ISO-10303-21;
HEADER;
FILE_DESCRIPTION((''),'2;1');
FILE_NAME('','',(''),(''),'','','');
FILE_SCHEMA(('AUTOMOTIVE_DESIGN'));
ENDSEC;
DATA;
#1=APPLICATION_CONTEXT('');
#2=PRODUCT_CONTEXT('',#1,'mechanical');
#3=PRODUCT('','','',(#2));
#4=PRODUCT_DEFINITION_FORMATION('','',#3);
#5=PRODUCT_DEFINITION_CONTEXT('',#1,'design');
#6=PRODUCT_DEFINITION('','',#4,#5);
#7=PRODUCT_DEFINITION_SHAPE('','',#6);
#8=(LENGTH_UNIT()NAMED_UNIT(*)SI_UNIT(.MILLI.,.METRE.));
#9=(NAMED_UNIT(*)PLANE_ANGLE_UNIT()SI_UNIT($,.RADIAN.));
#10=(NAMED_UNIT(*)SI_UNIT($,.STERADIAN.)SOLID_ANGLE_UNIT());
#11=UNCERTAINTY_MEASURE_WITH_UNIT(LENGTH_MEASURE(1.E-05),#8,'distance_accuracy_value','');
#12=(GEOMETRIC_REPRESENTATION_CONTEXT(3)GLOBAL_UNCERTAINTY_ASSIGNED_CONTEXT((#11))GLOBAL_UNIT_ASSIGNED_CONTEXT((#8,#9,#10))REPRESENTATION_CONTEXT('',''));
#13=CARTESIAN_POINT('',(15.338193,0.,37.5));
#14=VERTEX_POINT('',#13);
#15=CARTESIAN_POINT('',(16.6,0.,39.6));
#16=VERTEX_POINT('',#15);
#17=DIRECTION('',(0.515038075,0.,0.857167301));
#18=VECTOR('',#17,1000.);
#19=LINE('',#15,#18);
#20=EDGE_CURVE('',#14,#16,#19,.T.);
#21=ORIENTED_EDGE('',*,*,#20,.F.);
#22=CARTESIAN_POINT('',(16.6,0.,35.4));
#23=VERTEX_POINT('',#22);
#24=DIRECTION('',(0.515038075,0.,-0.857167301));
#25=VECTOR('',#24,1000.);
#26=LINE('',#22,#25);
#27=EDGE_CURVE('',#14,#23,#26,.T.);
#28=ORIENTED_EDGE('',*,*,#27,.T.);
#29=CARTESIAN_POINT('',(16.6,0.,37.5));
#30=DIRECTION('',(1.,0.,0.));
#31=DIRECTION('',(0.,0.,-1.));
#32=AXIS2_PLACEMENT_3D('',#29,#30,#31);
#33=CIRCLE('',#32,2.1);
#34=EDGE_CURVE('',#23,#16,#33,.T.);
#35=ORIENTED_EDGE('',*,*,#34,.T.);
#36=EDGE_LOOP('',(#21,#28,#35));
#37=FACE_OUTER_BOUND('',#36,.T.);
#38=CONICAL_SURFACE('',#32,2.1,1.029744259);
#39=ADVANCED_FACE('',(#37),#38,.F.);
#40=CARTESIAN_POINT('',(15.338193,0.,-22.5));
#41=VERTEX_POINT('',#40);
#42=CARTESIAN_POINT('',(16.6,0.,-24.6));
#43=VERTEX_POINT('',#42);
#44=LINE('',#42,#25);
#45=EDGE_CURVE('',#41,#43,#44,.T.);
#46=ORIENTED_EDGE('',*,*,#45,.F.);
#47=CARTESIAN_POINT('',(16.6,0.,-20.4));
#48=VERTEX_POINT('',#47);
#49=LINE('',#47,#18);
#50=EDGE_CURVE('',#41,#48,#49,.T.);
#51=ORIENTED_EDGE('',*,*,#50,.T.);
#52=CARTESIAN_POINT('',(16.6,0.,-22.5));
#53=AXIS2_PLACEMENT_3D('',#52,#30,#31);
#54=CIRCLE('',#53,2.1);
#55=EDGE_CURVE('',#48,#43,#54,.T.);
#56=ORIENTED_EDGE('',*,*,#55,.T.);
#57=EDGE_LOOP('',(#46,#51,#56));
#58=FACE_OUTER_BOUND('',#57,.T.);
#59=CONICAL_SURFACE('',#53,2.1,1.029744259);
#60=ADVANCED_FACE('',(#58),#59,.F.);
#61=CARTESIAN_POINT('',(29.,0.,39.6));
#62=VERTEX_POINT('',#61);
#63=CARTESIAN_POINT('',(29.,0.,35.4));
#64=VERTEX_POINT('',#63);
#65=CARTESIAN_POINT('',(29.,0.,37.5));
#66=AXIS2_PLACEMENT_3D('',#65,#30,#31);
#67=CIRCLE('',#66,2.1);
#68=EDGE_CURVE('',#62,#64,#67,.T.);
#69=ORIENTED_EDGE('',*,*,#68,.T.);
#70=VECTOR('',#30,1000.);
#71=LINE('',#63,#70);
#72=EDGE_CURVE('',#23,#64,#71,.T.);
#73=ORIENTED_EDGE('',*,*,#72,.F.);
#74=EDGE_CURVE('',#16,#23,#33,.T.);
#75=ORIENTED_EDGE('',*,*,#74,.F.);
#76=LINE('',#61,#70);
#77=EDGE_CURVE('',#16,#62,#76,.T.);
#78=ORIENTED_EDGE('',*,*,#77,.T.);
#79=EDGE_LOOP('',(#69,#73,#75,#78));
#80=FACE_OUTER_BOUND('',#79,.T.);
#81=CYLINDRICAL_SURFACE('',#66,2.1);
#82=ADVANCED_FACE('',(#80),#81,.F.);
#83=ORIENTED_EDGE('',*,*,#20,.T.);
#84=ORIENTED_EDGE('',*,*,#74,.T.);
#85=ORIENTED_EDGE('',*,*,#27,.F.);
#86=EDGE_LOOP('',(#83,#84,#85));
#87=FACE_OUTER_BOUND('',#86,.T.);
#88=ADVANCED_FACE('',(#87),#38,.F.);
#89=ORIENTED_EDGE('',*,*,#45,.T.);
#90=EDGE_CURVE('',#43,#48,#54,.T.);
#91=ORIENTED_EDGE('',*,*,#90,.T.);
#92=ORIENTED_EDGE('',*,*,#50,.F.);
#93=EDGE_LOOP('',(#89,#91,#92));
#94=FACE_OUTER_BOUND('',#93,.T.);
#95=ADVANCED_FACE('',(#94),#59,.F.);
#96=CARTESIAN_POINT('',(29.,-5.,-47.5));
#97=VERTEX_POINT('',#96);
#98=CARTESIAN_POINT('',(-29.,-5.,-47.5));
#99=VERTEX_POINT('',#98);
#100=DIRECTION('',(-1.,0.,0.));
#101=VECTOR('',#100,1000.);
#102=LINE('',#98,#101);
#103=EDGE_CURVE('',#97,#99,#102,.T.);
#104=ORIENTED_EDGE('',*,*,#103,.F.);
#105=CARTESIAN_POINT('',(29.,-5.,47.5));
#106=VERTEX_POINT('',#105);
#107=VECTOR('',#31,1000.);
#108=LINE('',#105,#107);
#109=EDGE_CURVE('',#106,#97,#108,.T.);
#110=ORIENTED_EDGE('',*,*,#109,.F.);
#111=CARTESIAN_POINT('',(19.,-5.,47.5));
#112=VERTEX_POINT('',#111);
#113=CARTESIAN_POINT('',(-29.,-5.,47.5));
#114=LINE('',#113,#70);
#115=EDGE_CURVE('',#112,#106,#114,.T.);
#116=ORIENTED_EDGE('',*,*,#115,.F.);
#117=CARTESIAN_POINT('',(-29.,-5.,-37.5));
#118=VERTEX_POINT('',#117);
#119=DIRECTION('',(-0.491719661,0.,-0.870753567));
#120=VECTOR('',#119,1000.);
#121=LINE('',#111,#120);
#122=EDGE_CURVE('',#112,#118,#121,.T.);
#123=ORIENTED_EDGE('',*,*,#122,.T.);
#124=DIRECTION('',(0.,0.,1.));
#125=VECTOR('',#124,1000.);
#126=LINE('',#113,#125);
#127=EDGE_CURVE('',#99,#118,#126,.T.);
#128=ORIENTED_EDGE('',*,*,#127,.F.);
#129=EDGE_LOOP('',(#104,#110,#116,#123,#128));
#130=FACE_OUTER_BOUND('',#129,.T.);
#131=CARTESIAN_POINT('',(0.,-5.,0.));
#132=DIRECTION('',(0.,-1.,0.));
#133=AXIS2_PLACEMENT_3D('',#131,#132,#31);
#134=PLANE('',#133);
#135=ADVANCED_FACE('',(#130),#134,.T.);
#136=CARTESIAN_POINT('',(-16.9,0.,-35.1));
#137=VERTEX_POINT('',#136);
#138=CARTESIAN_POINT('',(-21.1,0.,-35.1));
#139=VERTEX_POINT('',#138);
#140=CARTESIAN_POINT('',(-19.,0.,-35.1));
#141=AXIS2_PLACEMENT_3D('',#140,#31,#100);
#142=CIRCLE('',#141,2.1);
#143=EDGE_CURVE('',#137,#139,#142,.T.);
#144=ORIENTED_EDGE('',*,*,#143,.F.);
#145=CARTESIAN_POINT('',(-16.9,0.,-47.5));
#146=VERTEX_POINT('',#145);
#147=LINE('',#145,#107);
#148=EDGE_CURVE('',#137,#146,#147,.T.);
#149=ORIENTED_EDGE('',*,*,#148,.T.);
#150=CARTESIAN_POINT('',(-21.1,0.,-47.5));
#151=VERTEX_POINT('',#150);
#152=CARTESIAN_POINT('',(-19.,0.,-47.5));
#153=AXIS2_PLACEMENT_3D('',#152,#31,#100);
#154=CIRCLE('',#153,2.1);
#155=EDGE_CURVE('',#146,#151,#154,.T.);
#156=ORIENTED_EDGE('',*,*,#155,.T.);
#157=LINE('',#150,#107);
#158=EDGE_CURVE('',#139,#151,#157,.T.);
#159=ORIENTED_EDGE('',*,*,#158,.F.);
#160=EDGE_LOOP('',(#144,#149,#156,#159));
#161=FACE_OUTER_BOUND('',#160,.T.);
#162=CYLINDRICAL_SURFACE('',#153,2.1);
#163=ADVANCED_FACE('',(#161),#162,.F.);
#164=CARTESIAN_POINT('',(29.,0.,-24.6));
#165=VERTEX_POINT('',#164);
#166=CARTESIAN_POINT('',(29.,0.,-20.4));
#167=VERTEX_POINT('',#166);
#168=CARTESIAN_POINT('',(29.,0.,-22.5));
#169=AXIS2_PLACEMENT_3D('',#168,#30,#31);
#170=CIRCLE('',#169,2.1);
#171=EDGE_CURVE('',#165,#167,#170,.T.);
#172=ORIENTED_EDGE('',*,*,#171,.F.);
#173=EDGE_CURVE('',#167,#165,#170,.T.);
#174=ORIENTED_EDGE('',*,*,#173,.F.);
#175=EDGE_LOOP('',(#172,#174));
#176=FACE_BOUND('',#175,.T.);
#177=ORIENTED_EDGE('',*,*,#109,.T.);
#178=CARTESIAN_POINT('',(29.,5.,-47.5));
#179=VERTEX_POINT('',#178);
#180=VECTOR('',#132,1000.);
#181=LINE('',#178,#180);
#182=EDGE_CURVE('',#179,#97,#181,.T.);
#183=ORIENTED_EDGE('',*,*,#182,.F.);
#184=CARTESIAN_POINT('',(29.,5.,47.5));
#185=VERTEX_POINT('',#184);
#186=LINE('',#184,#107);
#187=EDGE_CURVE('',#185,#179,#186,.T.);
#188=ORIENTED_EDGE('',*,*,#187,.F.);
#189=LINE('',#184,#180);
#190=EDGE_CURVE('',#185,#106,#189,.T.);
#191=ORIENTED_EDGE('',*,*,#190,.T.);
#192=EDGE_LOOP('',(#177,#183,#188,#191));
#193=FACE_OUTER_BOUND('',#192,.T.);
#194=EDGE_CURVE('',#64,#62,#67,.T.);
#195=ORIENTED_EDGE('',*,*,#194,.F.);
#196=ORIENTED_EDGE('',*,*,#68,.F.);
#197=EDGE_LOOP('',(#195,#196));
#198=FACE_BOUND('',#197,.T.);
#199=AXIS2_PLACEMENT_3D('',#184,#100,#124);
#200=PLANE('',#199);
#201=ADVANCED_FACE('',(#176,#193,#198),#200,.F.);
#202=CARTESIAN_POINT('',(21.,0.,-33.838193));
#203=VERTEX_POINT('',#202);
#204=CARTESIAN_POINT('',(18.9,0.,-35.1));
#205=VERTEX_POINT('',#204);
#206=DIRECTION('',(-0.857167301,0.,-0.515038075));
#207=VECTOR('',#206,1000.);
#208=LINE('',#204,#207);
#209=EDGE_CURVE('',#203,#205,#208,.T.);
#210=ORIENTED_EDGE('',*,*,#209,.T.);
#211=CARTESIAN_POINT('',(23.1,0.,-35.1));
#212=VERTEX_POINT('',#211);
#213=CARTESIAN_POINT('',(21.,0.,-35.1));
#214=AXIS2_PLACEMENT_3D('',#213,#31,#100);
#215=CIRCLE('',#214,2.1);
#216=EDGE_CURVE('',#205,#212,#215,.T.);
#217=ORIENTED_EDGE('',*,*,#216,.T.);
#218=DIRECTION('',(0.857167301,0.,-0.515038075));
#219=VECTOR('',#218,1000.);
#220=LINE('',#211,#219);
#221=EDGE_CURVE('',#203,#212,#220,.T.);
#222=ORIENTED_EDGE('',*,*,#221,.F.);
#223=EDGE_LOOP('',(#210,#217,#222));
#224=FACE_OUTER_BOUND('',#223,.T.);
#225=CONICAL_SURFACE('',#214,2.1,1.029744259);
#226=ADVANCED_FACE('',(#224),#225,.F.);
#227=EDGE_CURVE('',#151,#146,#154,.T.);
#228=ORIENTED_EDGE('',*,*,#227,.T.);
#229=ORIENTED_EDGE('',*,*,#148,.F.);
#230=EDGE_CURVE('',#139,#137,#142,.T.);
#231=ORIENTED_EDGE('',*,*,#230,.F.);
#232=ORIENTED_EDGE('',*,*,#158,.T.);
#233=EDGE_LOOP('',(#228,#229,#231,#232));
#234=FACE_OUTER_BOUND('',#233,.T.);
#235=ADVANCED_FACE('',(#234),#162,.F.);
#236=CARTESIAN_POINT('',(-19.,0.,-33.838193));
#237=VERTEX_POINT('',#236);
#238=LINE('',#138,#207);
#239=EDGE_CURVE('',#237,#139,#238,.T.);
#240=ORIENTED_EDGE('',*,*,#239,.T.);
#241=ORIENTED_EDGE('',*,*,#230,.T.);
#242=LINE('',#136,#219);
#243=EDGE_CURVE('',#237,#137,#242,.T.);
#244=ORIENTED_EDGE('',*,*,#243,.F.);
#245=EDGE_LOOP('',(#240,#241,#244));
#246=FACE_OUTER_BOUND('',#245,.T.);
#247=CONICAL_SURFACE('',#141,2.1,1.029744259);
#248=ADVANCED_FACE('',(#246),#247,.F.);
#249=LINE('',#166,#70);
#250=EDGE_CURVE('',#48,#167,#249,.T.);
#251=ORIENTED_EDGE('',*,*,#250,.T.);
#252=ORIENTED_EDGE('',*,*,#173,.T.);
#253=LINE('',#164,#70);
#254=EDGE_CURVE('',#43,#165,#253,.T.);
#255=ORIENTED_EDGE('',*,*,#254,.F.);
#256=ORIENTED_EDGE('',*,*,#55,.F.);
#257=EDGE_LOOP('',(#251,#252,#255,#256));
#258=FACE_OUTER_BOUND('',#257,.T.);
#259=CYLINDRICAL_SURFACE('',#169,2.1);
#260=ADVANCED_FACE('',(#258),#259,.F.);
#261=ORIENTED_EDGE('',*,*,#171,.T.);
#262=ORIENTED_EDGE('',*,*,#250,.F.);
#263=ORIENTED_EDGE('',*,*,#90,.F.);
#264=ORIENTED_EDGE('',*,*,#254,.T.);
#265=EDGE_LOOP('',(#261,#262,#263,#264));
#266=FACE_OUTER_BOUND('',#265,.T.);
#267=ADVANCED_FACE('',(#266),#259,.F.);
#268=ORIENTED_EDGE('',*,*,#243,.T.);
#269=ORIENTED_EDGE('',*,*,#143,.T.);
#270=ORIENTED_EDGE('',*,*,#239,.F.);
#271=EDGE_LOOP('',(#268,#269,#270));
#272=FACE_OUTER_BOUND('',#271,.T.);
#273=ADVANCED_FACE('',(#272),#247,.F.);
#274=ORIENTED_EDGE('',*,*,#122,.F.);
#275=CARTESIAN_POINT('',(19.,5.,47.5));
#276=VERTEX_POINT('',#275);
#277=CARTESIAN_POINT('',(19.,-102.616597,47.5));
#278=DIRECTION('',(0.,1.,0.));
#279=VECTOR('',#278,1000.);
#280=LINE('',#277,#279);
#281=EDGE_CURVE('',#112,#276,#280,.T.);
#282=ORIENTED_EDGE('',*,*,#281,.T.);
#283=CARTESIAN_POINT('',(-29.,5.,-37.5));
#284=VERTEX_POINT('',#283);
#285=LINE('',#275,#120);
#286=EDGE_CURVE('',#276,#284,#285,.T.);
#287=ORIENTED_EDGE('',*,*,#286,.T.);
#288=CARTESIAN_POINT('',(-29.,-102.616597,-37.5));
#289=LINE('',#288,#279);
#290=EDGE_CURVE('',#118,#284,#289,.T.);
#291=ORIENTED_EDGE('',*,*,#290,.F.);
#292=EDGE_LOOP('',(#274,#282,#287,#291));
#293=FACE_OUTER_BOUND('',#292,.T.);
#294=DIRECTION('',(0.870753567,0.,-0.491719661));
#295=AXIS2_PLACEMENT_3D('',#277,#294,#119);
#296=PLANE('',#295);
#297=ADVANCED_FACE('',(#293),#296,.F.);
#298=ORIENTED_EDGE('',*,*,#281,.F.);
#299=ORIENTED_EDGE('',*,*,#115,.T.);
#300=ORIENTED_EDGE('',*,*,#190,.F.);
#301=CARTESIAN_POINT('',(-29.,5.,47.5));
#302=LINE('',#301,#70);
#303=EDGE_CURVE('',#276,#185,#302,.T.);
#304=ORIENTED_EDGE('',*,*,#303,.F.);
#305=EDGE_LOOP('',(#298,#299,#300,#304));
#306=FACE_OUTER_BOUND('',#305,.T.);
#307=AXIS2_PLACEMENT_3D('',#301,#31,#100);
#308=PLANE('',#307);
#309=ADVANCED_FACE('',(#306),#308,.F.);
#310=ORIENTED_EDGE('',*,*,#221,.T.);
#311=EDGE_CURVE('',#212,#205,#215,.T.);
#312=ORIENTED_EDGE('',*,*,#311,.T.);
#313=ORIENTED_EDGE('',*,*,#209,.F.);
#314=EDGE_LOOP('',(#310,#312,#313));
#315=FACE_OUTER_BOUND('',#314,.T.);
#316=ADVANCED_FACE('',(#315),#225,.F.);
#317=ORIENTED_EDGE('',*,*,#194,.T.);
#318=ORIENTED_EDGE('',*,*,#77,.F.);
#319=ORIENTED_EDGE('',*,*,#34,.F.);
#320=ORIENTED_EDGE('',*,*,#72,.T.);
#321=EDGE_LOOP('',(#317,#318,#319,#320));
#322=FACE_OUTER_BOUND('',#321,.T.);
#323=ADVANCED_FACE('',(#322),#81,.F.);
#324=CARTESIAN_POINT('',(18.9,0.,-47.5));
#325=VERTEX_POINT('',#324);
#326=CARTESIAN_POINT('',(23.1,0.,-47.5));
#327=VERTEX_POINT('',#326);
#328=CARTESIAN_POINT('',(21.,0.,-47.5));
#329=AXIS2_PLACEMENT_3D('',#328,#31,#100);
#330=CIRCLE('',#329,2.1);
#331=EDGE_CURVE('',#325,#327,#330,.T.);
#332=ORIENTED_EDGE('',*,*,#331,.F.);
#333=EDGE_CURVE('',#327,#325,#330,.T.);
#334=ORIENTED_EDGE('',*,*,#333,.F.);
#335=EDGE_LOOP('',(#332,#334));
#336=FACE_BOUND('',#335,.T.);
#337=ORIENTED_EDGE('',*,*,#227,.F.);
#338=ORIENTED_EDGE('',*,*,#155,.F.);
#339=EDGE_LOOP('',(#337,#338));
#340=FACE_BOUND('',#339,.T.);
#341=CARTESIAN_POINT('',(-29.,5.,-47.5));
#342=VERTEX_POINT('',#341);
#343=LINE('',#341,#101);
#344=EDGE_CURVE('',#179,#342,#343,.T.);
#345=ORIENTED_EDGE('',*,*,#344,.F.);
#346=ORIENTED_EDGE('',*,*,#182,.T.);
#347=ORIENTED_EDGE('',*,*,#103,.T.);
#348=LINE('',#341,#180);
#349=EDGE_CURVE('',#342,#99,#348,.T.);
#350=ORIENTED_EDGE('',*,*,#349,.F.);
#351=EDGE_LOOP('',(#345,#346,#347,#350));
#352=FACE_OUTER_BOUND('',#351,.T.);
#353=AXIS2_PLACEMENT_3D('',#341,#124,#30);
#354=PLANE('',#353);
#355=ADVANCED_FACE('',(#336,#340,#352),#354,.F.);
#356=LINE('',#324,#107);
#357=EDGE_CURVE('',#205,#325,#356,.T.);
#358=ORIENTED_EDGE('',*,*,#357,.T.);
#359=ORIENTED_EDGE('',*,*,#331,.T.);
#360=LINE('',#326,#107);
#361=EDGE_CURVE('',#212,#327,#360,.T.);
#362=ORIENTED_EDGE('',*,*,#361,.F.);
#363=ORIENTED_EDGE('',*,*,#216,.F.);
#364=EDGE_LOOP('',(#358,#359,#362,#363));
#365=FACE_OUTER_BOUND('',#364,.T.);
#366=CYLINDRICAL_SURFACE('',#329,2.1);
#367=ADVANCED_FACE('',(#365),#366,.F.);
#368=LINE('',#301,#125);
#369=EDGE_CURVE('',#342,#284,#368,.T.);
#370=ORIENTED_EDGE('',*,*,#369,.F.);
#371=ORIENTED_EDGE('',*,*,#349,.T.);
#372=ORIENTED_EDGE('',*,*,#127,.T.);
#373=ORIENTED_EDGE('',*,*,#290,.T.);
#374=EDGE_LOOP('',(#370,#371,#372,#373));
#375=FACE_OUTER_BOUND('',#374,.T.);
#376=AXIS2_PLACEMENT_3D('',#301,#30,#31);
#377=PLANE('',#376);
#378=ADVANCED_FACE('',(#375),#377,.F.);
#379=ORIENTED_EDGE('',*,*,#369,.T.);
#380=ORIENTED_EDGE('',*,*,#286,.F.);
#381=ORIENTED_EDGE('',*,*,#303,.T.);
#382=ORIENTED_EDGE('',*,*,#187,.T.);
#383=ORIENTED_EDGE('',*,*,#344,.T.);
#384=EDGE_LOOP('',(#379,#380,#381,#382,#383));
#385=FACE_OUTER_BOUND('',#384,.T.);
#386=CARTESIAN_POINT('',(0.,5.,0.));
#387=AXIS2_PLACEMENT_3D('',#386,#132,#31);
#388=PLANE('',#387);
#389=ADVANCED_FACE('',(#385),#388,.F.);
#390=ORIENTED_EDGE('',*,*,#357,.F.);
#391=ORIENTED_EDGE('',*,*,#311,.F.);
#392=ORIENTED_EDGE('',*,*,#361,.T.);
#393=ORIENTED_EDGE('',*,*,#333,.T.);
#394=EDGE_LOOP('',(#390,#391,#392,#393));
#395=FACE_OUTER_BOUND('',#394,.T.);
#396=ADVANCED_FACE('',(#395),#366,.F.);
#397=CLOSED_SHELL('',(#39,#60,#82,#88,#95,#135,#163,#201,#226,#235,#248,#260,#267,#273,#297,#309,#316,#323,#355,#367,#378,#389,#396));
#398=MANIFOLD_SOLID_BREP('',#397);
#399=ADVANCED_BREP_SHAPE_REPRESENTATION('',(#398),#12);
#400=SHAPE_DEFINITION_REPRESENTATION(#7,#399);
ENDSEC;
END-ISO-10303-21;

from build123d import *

# Parameters (mm, degrees)
SKETCH_1_W             = 58
SKETCH_1_H             = 95
EXTRUDE_1_DEPTH        = 5
CUT_EXTRUDE_1_DEPTH    = 10
HOLE_WIZARD_M5_1_D     = 4.2
HOLE_WIZARD_M5_1_DEPTH = 12.4
HOLE_WIZARD_M5_1_TIP   = 1.2618073
HOLE_WIZARD_M5_2_D     = 4.2
HOLE_WIZARD_M5_2_DEPTH = 12.4
HOLE_WIZARD_M5_2_TIP   = 1.2618073


with BuildPart() as part:
    # 草图1 → 凸台-拉伸1 (new, symmetric)
    with BuildSketch(Plane(origin=(0, 0, 0), x_dir=(1, 0, 0), z_dir=(0, 1, 0))):
        Rectangle(SKETCH_1_W, SKETCH_1_H)
    extrude(amount=EXTRUDE_1_DEPTH, both=True)

    # 草图2 → 切除-拉伸1 (cut)
    with BuildSketch(Plane(origin=(0, 5, 0), x_dir=(1, 0, 0), z_dir=(0, 1, 0))):
        Polygon((19, -47.5), (-29, 37.5), (-29, -47.5), align=None)
    extrude(amount=-CUT_EXTRUDE_1_DEPTH, mode=Mode.SUBTRACT)

    # M5 螺纹孔1
    with Locations(Plane(origin=(29, 0, 0), x_dir=(0, 0, -1), z_dir=(1, 0, 0))):
        with Locations((-37.5, 0), (22.5, 0)):
            Hole(HOLE_WIZARD_M5_1_D / 2, depth=HOLE_WIZARD_M5_1_DEPTH)
            with Locations((0, 0, -(HOLE_WIZARD_M5_1_DEPTH + HOLE_WIZARD_M5_1_TIP / 2))):  # 118° drill point
                Cone(0, HOLE_WIZARD_M5_1_D / 2, HOLE_WIZARD_M5_1_TIP, mode=Mode.SUBTRACT)

    # M5 螺纹孔2
    with Locations(Plane(origin=(0, 0, -47.5), x_dir=(-1, 0, 0), z_dir=(0, 0, -1))):
        with Locations((19, 0), (-21, 0)):
            Hole(HOLE_WIZARD_M5_2_D / 2, depth=HOLE_WIZARD_M5_2_DEPTH)
            with Locations((0, 0, -(HOLE_WIZARD_M5_2_DEPTH + HOLE_WIZARD_M5_2_TIP / 2))):  # 118° drill point
                Cone(0, HOLE_WIZARD_M5_2_D / 2, HOLE_WIZARD_M5_2_TIP, mode=Mode.SUBTRACT)


solid = part.part
